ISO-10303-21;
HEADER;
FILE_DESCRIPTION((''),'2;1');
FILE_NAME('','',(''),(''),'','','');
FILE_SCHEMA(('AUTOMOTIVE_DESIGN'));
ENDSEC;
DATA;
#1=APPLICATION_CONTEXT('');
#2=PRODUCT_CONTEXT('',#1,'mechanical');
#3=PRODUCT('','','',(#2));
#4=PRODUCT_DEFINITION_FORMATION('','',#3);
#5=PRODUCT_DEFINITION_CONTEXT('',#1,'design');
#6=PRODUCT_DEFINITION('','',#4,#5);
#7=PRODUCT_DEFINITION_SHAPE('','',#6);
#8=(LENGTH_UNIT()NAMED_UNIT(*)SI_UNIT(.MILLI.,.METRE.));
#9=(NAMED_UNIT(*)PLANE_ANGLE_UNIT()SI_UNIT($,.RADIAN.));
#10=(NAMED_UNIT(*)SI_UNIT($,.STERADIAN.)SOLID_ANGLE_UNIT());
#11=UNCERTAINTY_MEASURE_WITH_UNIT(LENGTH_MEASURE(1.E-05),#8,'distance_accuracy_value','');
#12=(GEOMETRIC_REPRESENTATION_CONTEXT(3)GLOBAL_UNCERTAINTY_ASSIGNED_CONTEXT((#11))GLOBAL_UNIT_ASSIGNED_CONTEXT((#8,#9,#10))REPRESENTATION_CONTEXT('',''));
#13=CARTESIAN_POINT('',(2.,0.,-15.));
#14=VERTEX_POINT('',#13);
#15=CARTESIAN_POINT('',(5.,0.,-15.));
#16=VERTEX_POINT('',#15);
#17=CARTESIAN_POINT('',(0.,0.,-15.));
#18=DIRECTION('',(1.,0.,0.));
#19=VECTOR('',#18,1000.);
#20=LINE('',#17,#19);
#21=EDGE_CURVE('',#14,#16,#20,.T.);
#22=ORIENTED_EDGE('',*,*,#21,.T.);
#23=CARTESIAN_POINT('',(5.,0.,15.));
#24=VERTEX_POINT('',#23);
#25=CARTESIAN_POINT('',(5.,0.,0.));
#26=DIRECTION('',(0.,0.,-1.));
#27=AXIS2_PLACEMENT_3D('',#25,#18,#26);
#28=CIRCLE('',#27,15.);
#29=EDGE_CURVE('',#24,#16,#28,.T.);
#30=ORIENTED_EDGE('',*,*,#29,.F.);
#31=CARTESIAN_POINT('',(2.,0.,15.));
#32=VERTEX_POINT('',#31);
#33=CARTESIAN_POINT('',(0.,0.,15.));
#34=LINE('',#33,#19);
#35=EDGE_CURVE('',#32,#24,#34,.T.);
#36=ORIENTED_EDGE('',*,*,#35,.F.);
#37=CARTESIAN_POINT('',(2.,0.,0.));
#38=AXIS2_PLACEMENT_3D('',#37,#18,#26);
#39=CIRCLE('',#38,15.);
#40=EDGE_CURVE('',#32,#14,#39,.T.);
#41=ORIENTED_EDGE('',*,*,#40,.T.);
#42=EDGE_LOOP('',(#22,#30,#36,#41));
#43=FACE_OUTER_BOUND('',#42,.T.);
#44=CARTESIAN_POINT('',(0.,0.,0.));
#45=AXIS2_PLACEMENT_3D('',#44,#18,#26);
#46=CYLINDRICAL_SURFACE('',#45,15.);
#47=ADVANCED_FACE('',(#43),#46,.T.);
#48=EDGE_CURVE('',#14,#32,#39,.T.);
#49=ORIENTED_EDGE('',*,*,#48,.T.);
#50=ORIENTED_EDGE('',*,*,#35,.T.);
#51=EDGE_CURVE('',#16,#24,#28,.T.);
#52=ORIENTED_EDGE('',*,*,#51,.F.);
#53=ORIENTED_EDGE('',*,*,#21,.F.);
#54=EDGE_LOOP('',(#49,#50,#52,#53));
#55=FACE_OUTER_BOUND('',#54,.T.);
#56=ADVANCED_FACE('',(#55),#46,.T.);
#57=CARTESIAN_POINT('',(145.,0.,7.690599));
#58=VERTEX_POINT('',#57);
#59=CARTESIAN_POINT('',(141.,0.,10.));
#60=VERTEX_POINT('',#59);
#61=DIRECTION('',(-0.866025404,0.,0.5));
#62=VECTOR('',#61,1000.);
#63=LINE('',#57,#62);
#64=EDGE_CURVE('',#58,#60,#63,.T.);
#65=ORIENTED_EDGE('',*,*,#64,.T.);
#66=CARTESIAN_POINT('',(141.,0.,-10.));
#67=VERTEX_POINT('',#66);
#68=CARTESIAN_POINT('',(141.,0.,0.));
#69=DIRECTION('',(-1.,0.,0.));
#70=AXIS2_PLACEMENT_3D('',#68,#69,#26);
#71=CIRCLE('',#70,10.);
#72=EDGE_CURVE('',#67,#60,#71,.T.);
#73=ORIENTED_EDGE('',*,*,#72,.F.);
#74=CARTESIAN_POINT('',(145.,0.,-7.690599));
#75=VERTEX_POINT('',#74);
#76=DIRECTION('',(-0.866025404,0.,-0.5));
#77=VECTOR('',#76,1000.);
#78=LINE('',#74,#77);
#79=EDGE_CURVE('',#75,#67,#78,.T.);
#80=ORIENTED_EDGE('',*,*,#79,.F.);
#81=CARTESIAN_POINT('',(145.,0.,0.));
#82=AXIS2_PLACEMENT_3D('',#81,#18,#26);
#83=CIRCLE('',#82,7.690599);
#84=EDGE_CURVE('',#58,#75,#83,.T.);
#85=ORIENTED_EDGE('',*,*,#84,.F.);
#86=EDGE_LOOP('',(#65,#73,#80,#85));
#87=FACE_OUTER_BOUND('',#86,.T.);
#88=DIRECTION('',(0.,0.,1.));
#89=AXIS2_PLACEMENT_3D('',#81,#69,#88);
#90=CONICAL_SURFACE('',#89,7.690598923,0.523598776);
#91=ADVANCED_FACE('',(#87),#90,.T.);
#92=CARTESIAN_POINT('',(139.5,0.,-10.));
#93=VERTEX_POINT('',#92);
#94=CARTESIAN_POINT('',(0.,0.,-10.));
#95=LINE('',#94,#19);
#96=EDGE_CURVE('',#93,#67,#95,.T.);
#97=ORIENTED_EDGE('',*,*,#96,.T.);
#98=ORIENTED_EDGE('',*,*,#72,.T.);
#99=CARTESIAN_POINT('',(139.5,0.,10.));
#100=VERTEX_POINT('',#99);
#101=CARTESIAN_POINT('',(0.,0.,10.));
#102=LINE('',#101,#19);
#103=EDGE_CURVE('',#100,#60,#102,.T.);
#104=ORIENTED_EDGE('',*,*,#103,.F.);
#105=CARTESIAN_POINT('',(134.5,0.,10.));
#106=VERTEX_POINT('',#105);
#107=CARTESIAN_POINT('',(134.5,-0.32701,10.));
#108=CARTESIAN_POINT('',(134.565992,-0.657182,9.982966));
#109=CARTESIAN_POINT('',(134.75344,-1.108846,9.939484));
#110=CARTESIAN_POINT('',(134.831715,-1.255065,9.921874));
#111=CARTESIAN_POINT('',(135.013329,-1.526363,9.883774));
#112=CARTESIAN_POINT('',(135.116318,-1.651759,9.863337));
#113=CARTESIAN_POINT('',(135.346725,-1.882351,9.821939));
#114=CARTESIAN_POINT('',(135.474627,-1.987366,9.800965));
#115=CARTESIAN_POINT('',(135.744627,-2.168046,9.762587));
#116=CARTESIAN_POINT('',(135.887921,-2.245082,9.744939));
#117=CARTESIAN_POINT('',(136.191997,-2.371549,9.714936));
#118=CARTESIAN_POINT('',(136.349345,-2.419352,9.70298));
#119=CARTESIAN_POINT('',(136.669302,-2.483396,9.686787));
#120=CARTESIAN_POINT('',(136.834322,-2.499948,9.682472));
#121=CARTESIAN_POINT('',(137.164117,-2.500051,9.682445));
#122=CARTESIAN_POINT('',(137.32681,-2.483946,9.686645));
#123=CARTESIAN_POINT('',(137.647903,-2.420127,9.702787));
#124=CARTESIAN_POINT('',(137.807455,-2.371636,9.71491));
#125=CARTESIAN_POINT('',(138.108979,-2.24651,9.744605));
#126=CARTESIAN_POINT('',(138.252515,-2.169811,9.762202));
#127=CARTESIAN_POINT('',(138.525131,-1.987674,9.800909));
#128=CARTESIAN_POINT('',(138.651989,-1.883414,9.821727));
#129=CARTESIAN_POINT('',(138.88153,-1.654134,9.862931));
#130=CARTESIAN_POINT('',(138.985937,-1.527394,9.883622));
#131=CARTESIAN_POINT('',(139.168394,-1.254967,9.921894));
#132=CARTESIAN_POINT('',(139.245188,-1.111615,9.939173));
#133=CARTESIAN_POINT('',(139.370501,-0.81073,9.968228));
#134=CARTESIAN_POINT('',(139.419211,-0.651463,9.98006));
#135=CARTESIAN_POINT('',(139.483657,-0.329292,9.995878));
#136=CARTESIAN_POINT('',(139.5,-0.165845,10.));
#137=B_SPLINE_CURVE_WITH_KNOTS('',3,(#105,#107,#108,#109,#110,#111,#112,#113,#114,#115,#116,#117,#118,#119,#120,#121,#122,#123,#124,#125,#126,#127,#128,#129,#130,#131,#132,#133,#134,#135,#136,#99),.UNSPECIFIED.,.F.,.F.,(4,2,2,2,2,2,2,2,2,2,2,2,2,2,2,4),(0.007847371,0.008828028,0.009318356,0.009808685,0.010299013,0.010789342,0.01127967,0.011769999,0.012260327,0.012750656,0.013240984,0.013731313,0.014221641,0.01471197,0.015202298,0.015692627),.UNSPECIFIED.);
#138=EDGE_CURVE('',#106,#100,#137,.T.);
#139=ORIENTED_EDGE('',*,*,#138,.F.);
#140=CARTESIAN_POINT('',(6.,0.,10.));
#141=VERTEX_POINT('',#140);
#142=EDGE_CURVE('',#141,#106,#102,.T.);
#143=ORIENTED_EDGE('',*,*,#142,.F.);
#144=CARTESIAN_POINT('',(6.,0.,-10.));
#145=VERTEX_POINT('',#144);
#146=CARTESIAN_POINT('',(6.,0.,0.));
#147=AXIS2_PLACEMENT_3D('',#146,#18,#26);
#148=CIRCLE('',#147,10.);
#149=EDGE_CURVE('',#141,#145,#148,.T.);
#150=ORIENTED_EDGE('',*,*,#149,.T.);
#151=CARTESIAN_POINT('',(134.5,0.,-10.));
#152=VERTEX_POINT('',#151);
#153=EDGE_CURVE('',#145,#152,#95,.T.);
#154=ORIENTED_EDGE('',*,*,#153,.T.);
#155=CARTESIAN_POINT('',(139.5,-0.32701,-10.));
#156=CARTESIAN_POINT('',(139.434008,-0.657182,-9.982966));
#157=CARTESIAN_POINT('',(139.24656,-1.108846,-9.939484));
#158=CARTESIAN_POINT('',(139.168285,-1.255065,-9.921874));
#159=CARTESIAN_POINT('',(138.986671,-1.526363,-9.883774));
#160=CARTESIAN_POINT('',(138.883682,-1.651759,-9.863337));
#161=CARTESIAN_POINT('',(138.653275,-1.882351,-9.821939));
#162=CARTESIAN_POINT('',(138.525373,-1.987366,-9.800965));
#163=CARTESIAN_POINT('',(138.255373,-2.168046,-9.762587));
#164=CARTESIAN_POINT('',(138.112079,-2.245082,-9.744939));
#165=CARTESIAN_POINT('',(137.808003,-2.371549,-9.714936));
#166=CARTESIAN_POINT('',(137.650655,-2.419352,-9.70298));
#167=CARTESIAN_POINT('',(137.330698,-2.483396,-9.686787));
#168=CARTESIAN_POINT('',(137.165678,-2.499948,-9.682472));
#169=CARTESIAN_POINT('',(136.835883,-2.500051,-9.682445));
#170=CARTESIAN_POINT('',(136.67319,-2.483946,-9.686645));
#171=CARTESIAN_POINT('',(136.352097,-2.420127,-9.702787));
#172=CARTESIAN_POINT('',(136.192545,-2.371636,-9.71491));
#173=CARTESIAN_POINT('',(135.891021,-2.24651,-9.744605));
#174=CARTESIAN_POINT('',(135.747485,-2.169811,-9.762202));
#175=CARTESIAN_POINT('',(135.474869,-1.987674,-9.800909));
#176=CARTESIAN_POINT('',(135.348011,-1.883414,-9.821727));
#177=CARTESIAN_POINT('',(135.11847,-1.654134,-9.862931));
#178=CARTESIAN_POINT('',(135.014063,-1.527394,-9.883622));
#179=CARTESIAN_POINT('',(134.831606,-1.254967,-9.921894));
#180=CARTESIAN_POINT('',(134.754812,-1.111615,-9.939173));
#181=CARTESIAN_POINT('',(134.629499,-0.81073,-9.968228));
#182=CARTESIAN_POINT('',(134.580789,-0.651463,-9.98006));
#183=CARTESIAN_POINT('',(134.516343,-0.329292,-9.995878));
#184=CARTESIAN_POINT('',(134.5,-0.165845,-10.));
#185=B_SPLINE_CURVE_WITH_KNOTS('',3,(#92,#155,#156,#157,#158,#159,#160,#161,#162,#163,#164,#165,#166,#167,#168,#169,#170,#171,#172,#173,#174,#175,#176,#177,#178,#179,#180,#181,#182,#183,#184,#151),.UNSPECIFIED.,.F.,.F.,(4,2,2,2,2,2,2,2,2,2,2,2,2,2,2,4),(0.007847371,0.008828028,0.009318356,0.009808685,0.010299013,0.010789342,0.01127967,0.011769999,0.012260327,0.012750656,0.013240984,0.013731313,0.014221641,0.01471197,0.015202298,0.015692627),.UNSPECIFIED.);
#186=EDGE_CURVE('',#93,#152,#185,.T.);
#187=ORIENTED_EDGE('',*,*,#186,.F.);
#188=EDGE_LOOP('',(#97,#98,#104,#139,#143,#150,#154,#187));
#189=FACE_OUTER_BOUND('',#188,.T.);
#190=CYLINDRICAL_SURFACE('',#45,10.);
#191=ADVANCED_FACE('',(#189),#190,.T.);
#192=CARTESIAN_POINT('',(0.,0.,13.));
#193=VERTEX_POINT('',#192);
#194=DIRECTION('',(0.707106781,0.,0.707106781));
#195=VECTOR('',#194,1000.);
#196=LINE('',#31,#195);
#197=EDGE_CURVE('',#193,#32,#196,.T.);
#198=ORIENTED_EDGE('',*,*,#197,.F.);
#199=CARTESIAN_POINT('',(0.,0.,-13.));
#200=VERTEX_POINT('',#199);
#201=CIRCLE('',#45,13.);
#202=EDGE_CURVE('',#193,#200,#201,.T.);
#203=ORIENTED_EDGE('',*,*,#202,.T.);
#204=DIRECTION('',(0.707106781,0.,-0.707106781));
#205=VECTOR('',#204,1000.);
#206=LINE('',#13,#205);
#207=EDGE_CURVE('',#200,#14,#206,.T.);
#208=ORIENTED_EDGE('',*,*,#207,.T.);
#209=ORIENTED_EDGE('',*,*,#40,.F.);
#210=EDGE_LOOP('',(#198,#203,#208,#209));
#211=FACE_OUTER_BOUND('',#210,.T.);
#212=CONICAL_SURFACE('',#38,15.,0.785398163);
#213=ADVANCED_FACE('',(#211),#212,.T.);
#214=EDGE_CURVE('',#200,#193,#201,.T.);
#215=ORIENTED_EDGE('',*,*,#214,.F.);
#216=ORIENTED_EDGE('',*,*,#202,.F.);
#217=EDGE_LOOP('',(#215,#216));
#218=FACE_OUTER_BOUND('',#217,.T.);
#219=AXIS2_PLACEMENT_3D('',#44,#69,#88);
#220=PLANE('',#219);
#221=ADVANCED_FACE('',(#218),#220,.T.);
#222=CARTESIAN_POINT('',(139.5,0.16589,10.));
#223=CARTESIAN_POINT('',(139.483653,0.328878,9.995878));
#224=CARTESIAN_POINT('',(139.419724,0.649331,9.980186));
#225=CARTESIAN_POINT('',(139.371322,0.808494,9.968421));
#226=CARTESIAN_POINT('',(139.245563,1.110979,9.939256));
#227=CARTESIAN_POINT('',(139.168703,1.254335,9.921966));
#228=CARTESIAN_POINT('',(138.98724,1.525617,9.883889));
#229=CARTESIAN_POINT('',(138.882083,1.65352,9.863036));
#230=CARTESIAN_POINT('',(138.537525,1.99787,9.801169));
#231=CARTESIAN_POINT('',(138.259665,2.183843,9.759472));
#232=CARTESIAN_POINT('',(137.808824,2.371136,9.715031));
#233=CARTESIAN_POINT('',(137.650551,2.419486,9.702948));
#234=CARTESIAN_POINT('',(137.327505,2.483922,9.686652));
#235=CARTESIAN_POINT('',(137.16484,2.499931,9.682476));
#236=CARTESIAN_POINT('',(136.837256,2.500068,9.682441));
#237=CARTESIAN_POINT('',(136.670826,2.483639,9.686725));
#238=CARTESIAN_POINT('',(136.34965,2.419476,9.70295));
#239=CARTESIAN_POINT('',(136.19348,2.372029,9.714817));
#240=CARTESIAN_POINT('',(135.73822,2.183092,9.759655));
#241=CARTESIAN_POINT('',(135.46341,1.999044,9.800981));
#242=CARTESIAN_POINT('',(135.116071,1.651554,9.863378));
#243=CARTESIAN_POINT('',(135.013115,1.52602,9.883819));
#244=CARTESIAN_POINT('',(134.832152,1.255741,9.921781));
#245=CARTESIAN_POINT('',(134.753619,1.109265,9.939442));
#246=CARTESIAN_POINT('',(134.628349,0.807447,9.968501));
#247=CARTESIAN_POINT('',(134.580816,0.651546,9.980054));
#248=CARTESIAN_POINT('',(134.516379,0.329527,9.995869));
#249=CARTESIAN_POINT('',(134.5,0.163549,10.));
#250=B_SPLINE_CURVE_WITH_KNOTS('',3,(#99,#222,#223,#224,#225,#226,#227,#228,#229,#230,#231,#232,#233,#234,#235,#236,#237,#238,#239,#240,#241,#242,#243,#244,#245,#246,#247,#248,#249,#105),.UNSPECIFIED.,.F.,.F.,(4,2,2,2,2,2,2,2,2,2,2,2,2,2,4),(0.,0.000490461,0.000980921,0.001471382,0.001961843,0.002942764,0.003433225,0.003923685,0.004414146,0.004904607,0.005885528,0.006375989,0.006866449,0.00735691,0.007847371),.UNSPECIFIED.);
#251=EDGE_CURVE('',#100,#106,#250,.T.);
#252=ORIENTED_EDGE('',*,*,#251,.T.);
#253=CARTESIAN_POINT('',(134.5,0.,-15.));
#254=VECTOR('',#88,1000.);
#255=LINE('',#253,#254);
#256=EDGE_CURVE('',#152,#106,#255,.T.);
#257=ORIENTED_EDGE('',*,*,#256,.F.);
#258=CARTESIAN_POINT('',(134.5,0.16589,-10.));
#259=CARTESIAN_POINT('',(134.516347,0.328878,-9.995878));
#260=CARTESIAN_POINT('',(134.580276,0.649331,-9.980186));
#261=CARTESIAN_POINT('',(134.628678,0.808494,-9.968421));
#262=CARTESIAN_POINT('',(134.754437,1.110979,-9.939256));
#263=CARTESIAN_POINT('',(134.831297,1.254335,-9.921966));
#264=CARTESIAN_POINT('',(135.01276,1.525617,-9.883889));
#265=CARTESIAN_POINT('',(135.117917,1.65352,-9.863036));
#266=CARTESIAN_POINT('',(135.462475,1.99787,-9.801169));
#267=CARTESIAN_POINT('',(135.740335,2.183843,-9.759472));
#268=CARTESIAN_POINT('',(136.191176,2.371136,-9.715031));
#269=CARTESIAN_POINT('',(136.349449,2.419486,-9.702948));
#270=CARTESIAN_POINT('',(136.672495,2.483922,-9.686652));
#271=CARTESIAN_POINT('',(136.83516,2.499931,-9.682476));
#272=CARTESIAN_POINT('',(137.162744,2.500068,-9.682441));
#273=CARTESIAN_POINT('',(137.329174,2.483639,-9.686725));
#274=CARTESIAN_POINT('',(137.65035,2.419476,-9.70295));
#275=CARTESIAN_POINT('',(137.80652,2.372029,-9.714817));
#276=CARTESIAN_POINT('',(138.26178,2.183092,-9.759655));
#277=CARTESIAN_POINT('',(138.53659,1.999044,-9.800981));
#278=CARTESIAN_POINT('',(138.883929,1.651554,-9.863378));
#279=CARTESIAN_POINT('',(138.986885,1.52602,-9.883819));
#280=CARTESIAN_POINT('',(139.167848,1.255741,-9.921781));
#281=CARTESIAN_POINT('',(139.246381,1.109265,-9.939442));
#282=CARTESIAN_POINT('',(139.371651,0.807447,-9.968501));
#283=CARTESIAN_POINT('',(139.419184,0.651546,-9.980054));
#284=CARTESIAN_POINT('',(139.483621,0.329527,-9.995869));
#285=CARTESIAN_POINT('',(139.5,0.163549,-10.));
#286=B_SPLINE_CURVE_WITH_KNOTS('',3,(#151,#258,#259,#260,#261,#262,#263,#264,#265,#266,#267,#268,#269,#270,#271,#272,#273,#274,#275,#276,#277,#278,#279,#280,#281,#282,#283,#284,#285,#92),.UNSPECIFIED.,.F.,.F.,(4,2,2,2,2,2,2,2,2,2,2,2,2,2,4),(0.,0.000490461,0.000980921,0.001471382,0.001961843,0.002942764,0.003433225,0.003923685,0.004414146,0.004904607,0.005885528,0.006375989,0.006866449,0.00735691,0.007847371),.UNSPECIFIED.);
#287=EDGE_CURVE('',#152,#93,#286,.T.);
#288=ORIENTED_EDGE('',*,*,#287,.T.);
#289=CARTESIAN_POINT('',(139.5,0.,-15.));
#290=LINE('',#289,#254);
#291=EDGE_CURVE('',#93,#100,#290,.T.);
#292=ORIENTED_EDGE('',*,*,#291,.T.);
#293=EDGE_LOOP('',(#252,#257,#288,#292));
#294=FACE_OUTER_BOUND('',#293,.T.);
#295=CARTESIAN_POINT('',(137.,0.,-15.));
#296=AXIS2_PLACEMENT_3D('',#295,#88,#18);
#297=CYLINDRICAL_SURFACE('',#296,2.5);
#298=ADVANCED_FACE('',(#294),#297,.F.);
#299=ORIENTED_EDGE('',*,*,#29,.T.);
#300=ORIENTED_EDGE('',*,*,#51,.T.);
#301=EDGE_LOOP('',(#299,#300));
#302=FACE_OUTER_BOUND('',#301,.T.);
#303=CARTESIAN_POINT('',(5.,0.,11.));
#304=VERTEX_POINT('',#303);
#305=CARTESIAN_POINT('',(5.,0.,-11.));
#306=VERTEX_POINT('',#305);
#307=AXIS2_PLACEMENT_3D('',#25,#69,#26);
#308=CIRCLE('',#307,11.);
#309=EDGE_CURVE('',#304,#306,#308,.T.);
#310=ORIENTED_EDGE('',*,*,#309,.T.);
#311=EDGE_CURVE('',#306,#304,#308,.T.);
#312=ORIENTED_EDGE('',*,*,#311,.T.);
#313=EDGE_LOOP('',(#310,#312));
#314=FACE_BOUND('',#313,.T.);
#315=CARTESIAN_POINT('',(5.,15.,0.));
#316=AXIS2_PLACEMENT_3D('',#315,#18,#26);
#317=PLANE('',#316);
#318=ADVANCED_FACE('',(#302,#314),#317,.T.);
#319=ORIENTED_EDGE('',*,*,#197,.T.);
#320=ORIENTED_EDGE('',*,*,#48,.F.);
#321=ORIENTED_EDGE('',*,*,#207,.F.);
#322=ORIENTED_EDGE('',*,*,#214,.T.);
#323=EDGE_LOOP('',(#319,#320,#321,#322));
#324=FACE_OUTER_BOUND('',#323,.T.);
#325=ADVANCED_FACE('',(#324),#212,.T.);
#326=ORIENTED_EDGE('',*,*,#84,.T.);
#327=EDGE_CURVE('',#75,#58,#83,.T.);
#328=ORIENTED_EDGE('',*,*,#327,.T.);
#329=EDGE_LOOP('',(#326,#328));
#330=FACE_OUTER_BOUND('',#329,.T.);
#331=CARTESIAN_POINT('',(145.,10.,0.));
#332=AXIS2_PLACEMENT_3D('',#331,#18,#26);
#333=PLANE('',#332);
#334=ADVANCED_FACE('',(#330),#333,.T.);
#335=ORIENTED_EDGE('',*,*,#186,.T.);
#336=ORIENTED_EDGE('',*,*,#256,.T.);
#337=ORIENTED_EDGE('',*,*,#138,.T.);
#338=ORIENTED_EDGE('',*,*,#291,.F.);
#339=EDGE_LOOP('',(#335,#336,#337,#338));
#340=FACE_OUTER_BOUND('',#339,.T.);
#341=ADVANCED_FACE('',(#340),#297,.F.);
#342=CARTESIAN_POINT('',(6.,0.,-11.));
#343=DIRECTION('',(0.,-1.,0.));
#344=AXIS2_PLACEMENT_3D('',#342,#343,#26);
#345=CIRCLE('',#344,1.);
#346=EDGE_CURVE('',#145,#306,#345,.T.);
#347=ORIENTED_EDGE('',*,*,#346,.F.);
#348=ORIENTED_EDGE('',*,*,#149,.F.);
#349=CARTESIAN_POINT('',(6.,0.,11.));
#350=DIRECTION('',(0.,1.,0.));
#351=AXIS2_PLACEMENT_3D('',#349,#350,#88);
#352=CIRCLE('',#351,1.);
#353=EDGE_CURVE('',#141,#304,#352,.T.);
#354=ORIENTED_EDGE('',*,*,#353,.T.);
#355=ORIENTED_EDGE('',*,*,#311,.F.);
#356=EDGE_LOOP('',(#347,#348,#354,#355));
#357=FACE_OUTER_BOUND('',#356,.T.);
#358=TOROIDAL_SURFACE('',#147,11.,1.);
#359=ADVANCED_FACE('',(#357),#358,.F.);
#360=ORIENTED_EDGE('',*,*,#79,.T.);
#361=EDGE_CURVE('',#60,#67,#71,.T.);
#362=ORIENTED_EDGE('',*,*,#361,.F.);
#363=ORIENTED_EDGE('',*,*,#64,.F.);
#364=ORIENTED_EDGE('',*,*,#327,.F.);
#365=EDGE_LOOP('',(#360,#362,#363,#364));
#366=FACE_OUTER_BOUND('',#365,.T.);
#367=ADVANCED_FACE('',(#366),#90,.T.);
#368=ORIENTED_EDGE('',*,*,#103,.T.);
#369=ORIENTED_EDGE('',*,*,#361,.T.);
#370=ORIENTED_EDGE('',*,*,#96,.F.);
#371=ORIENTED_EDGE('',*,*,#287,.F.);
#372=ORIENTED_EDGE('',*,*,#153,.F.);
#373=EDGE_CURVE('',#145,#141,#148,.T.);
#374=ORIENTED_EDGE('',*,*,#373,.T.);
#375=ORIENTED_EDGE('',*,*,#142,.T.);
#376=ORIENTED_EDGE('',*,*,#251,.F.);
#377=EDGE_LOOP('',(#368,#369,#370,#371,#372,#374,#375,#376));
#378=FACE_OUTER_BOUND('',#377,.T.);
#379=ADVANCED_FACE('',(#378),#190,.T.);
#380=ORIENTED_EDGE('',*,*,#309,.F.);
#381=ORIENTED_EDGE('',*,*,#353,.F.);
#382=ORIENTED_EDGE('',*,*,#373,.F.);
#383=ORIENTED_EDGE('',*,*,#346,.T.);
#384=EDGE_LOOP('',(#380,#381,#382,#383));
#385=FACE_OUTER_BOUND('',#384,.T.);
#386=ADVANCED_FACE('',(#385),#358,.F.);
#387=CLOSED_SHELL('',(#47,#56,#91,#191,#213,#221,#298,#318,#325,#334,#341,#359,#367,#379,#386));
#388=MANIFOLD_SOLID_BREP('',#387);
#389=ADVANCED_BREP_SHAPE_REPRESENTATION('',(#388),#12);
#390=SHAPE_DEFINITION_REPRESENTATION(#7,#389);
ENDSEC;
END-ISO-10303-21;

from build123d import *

# Parameters (mm, degrees)
CUT_EXTRUDE_1_DEPTH      = 147.543508898
CUT_EXTRUDE_1_DEPTH_BACK = 147.543508898
SKETCH_2_R               = 2.5
FILLET_1_R               = 1
CHAMFER_1_SIZE           = 4
CHAMFER_1_SIZE2          = 2.309401077


with BuildPart() as part:
    # 草图1 → Revolve 546 (revolve)
    with BuildSketch(Plane.XY, mode=Mode.PRIVATE) as revolve_546_sk:
        Polygon((0, 0), (145, 0), (145, 10), (5, 10), (5, 15), (2, 15), (0, 13), align=None)
    revolve(revolve_546_sk.sketch.rotate(Axis((0, 0, 0), (-1, 0, 0)), 90), axis=Axis((0, 0, 0), (-1, 0, 0)))

    # 草图2 → 切除-拉伸1 (cut, two sides: drawn at the far end of the back side and taken through both)
    with BuildSketch(Plane.XY.offset(-CUT_EXTRUDE_1_DEPTH_BACK)):
        with Locations((137, 0)):
            Circle(SKETCH_2_R)
    extrude(amount=CUT_EXTRUDE_1_DEPTH + CUT_EXTRUDE_1_DEPTH_BACK, mode=Mode.SUBTRACT)

    # 圆角1
    fillet_1_edges = [part.edges().sort_by_distance(p)[0] for p in [
        (5, 0, 10),
    ]]
    fillet(fillet_1_edges, radius=FILLET_1_R)

    # 倒角1
    chamfer_1_edges = [part.edges().sort_by_distance(p)[0] for p in [
        (145, 0, 10),
    ]]
    chamfer_1_side = [part.faces().sort_by_distance(p)[0] for p in [
        (75.5, 0, 10),
    ]]
    chamfer(chamfer_1_edges, length=CHAMFER_1_SIZE, length2=CHAMFER_1_SIZE2, reference=chamfer_1_side[0])


solid = part.part
